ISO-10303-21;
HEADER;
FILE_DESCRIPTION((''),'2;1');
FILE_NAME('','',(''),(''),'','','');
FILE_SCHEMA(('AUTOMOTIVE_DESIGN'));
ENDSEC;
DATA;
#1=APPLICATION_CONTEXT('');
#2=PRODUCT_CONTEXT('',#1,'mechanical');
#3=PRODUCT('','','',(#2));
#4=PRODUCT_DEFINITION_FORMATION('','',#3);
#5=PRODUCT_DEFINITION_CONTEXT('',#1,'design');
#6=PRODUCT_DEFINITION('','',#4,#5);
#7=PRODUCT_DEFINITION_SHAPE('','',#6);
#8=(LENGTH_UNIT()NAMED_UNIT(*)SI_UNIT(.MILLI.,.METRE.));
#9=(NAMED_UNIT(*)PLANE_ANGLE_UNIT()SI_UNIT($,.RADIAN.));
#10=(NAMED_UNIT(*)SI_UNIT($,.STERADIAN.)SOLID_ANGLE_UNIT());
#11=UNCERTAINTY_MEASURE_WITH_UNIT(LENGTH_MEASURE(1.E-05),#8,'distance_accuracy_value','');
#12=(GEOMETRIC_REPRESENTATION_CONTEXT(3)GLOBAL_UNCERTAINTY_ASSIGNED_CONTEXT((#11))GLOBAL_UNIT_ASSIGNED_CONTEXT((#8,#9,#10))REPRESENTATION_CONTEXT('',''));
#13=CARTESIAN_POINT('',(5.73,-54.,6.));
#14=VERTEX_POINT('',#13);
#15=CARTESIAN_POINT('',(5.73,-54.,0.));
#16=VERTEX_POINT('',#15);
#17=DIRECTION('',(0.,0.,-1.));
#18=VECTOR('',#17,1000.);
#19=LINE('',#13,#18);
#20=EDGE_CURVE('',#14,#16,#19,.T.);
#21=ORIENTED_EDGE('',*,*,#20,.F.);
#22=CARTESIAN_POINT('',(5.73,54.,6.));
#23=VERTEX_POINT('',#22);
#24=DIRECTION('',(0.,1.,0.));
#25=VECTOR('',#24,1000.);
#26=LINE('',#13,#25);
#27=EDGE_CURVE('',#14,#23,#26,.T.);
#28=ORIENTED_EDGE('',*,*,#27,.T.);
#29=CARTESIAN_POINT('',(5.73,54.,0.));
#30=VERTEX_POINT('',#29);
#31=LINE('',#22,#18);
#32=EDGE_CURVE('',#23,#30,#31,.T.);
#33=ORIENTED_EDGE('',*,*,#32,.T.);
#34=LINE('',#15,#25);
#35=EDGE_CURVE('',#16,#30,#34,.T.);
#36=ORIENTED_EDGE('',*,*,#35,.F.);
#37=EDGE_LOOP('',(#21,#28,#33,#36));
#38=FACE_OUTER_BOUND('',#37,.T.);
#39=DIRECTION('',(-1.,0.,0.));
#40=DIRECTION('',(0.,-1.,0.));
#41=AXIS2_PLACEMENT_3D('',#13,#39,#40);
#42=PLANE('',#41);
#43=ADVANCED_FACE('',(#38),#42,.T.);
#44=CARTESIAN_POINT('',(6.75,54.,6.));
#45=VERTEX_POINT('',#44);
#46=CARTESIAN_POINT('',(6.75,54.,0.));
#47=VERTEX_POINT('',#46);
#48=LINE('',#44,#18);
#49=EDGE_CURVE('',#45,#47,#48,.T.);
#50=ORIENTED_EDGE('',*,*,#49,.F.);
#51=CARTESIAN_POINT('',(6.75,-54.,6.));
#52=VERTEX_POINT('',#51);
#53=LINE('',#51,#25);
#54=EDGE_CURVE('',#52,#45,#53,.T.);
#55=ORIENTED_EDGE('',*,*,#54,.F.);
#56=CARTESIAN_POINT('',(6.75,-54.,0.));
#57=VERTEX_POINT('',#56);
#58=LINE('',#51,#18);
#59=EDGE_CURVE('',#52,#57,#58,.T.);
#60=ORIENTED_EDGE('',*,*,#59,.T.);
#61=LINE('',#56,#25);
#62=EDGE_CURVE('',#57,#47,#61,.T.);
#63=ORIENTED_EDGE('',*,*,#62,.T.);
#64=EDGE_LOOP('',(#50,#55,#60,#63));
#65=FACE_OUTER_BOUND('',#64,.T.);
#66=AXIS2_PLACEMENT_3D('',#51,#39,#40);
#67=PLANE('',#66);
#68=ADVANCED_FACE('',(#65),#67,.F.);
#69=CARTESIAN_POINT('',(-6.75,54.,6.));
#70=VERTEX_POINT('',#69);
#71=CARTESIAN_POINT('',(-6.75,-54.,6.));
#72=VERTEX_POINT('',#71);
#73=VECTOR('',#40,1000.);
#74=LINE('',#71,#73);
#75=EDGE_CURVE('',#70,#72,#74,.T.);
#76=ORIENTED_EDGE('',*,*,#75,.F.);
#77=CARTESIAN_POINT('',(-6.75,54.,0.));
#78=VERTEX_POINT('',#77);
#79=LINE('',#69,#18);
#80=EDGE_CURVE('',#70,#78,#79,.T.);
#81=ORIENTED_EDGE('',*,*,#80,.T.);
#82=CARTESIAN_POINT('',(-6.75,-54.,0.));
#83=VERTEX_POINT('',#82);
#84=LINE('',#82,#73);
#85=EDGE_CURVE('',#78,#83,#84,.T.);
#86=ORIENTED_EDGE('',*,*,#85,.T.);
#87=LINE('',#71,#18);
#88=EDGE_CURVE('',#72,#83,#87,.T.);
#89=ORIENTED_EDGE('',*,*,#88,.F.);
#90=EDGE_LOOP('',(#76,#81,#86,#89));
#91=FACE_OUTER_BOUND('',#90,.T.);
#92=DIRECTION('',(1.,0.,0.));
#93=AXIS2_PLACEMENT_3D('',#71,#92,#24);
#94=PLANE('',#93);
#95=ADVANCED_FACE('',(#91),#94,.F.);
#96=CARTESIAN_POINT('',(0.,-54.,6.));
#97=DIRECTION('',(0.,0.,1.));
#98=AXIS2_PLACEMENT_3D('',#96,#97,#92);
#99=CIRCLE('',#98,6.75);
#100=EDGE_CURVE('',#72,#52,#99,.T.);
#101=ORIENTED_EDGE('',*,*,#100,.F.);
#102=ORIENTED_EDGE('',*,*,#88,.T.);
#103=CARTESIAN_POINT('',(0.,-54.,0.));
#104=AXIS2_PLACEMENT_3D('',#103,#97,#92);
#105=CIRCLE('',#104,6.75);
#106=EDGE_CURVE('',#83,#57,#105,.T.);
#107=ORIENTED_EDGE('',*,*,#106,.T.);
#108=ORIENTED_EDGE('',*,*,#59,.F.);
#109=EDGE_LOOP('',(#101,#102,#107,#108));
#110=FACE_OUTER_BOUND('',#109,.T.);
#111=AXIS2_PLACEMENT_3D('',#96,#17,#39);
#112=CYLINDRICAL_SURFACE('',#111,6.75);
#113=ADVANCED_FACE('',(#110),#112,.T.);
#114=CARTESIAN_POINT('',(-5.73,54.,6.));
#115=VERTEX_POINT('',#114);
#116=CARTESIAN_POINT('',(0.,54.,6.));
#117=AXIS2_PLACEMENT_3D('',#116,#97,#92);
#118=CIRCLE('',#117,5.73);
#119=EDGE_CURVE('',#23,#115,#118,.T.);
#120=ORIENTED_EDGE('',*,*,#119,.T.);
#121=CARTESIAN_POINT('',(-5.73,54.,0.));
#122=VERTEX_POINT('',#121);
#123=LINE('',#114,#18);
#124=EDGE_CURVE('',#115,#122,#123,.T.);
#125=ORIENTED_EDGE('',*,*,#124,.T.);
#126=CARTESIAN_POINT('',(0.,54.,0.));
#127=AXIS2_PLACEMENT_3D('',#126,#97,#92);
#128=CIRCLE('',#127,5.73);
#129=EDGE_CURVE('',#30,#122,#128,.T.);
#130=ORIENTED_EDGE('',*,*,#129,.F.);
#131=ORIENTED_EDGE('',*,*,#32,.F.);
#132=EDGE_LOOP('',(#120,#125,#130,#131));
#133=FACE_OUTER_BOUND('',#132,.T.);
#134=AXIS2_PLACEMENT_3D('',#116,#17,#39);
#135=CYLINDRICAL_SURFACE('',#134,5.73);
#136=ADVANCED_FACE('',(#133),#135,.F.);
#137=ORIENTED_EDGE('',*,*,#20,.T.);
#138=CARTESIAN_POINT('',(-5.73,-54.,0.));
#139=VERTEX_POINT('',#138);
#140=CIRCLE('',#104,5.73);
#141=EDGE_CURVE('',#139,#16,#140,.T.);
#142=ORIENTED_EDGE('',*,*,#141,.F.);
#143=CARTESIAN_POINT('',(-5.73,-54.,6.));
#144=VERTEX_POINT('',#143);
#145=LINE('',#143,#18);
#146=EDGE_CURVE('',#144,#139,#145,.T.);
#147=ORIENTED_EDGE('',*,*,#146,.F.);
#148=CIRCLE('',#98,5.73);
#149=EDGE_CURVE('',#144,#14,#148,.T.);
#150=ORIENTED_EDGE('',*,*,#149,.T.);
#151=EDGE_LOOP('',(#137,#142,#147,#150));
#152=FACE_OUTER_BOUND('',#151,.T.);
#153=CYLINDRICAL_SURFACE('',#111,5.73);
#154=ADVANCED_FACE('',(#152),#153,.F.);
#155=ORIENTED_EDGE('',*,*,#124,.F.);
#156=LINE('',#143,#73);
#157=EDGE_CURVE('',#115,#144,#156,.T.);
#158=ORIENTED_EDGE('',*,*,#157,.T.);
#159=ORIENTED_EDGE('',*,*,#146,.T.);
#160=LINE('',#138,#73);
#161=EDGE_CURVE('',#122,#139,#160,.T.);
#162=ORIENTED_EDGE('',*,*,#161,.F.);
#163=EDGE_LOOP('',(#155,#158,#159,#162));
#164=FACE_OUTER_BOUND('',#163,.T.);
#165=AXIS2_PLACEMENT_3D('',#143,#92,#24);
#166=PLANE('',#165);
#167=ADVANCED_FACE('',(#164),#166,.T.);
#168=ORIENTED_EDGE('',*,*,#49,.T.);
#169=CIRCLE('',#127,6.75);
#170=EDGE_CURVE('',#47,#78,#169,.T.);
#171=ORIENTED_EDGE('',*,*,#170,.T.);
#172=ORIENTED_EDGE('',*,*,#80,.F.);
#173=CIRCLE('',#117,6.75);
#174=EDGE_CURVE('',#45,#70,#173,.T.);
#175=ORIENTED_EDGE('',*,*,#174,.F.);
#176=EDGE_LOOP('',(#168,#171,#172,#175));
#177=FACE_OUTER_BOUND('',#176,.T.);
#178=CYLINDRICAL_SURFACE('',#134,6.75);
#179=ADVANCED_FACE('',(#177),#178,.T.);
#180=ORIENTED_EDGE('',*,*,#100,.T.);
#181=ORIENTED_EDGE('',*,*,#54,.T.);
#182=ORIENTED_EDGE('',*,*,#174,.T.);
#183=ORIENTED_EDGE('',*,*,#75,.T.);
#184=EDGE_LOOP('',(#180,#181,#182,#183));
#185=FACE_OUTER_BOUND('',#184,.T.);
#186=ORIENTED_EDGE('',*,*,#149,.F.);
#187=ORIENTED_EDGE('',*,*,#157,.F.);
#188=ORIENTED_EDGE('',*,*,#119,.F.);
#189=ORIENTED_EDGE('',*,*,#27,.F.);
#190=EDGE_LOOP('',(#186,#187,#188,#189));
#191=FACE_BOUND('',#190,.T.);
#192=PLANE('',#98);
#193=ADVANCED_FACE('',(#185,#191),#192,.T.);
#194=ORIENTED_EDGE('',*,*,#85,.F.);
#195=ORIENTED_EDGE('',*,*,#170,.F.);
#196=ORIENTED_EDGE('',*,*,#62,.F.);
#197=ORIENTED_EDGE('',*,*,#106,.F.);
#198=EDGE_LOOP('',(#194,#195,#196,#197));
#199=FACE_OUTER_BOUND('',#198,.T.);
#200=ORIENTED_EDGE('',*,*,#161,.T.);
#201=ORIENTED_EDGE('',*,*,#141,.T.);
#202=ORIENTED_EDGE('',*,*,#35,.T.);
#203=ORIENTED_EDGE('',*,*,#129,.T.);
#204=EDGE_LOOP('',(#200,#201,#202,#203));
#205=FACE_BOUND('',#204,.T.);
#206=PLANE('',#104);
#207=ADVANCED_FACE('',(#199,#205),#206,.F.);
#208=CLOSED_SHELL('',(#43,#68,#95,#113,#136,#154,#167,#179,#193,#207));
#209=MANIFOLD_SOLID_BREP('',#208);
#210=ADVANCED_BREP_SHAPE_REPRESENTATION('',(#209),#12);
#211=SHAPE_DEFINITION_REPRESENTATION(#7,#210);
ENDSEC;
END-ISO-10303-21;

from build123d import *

# Parameters (mm, degrees)
BOSS_EXTRUDE1_DEPTH = 6


with BuildPart() as part:
    # Sketch1 → Boss-Extrude1 (new body)
    with BuildSketch(Plane.XY):
        with BuildLine():
            Line((-6.75, -54), (-6.75, 54))
            ThreePointArc((-6.75, 54), (0, 60.75), (6.75, 54))
            Line((6.75, 54), (6.75, -54))
            ThreePointArc((6.75, -54), (0, -60.75), (-6.75, -54))
        make_face()
        with BuildLine():
            Line((-5.73, -54), (-5.73, 54))
            ThreePointArc((-5.73, 54), (0, 59.73), (5.73, 54))
            Line((5.73, 54), (5.73, -54))
            ThreePointArc((5.73, -54), (0, -59.73), (-5.73, -54))
        make_face(mode=Mode.SUBTRACT)
    extrude(amount=BOSS_EXTRUDE1_DEPTH)


solid = part.part
